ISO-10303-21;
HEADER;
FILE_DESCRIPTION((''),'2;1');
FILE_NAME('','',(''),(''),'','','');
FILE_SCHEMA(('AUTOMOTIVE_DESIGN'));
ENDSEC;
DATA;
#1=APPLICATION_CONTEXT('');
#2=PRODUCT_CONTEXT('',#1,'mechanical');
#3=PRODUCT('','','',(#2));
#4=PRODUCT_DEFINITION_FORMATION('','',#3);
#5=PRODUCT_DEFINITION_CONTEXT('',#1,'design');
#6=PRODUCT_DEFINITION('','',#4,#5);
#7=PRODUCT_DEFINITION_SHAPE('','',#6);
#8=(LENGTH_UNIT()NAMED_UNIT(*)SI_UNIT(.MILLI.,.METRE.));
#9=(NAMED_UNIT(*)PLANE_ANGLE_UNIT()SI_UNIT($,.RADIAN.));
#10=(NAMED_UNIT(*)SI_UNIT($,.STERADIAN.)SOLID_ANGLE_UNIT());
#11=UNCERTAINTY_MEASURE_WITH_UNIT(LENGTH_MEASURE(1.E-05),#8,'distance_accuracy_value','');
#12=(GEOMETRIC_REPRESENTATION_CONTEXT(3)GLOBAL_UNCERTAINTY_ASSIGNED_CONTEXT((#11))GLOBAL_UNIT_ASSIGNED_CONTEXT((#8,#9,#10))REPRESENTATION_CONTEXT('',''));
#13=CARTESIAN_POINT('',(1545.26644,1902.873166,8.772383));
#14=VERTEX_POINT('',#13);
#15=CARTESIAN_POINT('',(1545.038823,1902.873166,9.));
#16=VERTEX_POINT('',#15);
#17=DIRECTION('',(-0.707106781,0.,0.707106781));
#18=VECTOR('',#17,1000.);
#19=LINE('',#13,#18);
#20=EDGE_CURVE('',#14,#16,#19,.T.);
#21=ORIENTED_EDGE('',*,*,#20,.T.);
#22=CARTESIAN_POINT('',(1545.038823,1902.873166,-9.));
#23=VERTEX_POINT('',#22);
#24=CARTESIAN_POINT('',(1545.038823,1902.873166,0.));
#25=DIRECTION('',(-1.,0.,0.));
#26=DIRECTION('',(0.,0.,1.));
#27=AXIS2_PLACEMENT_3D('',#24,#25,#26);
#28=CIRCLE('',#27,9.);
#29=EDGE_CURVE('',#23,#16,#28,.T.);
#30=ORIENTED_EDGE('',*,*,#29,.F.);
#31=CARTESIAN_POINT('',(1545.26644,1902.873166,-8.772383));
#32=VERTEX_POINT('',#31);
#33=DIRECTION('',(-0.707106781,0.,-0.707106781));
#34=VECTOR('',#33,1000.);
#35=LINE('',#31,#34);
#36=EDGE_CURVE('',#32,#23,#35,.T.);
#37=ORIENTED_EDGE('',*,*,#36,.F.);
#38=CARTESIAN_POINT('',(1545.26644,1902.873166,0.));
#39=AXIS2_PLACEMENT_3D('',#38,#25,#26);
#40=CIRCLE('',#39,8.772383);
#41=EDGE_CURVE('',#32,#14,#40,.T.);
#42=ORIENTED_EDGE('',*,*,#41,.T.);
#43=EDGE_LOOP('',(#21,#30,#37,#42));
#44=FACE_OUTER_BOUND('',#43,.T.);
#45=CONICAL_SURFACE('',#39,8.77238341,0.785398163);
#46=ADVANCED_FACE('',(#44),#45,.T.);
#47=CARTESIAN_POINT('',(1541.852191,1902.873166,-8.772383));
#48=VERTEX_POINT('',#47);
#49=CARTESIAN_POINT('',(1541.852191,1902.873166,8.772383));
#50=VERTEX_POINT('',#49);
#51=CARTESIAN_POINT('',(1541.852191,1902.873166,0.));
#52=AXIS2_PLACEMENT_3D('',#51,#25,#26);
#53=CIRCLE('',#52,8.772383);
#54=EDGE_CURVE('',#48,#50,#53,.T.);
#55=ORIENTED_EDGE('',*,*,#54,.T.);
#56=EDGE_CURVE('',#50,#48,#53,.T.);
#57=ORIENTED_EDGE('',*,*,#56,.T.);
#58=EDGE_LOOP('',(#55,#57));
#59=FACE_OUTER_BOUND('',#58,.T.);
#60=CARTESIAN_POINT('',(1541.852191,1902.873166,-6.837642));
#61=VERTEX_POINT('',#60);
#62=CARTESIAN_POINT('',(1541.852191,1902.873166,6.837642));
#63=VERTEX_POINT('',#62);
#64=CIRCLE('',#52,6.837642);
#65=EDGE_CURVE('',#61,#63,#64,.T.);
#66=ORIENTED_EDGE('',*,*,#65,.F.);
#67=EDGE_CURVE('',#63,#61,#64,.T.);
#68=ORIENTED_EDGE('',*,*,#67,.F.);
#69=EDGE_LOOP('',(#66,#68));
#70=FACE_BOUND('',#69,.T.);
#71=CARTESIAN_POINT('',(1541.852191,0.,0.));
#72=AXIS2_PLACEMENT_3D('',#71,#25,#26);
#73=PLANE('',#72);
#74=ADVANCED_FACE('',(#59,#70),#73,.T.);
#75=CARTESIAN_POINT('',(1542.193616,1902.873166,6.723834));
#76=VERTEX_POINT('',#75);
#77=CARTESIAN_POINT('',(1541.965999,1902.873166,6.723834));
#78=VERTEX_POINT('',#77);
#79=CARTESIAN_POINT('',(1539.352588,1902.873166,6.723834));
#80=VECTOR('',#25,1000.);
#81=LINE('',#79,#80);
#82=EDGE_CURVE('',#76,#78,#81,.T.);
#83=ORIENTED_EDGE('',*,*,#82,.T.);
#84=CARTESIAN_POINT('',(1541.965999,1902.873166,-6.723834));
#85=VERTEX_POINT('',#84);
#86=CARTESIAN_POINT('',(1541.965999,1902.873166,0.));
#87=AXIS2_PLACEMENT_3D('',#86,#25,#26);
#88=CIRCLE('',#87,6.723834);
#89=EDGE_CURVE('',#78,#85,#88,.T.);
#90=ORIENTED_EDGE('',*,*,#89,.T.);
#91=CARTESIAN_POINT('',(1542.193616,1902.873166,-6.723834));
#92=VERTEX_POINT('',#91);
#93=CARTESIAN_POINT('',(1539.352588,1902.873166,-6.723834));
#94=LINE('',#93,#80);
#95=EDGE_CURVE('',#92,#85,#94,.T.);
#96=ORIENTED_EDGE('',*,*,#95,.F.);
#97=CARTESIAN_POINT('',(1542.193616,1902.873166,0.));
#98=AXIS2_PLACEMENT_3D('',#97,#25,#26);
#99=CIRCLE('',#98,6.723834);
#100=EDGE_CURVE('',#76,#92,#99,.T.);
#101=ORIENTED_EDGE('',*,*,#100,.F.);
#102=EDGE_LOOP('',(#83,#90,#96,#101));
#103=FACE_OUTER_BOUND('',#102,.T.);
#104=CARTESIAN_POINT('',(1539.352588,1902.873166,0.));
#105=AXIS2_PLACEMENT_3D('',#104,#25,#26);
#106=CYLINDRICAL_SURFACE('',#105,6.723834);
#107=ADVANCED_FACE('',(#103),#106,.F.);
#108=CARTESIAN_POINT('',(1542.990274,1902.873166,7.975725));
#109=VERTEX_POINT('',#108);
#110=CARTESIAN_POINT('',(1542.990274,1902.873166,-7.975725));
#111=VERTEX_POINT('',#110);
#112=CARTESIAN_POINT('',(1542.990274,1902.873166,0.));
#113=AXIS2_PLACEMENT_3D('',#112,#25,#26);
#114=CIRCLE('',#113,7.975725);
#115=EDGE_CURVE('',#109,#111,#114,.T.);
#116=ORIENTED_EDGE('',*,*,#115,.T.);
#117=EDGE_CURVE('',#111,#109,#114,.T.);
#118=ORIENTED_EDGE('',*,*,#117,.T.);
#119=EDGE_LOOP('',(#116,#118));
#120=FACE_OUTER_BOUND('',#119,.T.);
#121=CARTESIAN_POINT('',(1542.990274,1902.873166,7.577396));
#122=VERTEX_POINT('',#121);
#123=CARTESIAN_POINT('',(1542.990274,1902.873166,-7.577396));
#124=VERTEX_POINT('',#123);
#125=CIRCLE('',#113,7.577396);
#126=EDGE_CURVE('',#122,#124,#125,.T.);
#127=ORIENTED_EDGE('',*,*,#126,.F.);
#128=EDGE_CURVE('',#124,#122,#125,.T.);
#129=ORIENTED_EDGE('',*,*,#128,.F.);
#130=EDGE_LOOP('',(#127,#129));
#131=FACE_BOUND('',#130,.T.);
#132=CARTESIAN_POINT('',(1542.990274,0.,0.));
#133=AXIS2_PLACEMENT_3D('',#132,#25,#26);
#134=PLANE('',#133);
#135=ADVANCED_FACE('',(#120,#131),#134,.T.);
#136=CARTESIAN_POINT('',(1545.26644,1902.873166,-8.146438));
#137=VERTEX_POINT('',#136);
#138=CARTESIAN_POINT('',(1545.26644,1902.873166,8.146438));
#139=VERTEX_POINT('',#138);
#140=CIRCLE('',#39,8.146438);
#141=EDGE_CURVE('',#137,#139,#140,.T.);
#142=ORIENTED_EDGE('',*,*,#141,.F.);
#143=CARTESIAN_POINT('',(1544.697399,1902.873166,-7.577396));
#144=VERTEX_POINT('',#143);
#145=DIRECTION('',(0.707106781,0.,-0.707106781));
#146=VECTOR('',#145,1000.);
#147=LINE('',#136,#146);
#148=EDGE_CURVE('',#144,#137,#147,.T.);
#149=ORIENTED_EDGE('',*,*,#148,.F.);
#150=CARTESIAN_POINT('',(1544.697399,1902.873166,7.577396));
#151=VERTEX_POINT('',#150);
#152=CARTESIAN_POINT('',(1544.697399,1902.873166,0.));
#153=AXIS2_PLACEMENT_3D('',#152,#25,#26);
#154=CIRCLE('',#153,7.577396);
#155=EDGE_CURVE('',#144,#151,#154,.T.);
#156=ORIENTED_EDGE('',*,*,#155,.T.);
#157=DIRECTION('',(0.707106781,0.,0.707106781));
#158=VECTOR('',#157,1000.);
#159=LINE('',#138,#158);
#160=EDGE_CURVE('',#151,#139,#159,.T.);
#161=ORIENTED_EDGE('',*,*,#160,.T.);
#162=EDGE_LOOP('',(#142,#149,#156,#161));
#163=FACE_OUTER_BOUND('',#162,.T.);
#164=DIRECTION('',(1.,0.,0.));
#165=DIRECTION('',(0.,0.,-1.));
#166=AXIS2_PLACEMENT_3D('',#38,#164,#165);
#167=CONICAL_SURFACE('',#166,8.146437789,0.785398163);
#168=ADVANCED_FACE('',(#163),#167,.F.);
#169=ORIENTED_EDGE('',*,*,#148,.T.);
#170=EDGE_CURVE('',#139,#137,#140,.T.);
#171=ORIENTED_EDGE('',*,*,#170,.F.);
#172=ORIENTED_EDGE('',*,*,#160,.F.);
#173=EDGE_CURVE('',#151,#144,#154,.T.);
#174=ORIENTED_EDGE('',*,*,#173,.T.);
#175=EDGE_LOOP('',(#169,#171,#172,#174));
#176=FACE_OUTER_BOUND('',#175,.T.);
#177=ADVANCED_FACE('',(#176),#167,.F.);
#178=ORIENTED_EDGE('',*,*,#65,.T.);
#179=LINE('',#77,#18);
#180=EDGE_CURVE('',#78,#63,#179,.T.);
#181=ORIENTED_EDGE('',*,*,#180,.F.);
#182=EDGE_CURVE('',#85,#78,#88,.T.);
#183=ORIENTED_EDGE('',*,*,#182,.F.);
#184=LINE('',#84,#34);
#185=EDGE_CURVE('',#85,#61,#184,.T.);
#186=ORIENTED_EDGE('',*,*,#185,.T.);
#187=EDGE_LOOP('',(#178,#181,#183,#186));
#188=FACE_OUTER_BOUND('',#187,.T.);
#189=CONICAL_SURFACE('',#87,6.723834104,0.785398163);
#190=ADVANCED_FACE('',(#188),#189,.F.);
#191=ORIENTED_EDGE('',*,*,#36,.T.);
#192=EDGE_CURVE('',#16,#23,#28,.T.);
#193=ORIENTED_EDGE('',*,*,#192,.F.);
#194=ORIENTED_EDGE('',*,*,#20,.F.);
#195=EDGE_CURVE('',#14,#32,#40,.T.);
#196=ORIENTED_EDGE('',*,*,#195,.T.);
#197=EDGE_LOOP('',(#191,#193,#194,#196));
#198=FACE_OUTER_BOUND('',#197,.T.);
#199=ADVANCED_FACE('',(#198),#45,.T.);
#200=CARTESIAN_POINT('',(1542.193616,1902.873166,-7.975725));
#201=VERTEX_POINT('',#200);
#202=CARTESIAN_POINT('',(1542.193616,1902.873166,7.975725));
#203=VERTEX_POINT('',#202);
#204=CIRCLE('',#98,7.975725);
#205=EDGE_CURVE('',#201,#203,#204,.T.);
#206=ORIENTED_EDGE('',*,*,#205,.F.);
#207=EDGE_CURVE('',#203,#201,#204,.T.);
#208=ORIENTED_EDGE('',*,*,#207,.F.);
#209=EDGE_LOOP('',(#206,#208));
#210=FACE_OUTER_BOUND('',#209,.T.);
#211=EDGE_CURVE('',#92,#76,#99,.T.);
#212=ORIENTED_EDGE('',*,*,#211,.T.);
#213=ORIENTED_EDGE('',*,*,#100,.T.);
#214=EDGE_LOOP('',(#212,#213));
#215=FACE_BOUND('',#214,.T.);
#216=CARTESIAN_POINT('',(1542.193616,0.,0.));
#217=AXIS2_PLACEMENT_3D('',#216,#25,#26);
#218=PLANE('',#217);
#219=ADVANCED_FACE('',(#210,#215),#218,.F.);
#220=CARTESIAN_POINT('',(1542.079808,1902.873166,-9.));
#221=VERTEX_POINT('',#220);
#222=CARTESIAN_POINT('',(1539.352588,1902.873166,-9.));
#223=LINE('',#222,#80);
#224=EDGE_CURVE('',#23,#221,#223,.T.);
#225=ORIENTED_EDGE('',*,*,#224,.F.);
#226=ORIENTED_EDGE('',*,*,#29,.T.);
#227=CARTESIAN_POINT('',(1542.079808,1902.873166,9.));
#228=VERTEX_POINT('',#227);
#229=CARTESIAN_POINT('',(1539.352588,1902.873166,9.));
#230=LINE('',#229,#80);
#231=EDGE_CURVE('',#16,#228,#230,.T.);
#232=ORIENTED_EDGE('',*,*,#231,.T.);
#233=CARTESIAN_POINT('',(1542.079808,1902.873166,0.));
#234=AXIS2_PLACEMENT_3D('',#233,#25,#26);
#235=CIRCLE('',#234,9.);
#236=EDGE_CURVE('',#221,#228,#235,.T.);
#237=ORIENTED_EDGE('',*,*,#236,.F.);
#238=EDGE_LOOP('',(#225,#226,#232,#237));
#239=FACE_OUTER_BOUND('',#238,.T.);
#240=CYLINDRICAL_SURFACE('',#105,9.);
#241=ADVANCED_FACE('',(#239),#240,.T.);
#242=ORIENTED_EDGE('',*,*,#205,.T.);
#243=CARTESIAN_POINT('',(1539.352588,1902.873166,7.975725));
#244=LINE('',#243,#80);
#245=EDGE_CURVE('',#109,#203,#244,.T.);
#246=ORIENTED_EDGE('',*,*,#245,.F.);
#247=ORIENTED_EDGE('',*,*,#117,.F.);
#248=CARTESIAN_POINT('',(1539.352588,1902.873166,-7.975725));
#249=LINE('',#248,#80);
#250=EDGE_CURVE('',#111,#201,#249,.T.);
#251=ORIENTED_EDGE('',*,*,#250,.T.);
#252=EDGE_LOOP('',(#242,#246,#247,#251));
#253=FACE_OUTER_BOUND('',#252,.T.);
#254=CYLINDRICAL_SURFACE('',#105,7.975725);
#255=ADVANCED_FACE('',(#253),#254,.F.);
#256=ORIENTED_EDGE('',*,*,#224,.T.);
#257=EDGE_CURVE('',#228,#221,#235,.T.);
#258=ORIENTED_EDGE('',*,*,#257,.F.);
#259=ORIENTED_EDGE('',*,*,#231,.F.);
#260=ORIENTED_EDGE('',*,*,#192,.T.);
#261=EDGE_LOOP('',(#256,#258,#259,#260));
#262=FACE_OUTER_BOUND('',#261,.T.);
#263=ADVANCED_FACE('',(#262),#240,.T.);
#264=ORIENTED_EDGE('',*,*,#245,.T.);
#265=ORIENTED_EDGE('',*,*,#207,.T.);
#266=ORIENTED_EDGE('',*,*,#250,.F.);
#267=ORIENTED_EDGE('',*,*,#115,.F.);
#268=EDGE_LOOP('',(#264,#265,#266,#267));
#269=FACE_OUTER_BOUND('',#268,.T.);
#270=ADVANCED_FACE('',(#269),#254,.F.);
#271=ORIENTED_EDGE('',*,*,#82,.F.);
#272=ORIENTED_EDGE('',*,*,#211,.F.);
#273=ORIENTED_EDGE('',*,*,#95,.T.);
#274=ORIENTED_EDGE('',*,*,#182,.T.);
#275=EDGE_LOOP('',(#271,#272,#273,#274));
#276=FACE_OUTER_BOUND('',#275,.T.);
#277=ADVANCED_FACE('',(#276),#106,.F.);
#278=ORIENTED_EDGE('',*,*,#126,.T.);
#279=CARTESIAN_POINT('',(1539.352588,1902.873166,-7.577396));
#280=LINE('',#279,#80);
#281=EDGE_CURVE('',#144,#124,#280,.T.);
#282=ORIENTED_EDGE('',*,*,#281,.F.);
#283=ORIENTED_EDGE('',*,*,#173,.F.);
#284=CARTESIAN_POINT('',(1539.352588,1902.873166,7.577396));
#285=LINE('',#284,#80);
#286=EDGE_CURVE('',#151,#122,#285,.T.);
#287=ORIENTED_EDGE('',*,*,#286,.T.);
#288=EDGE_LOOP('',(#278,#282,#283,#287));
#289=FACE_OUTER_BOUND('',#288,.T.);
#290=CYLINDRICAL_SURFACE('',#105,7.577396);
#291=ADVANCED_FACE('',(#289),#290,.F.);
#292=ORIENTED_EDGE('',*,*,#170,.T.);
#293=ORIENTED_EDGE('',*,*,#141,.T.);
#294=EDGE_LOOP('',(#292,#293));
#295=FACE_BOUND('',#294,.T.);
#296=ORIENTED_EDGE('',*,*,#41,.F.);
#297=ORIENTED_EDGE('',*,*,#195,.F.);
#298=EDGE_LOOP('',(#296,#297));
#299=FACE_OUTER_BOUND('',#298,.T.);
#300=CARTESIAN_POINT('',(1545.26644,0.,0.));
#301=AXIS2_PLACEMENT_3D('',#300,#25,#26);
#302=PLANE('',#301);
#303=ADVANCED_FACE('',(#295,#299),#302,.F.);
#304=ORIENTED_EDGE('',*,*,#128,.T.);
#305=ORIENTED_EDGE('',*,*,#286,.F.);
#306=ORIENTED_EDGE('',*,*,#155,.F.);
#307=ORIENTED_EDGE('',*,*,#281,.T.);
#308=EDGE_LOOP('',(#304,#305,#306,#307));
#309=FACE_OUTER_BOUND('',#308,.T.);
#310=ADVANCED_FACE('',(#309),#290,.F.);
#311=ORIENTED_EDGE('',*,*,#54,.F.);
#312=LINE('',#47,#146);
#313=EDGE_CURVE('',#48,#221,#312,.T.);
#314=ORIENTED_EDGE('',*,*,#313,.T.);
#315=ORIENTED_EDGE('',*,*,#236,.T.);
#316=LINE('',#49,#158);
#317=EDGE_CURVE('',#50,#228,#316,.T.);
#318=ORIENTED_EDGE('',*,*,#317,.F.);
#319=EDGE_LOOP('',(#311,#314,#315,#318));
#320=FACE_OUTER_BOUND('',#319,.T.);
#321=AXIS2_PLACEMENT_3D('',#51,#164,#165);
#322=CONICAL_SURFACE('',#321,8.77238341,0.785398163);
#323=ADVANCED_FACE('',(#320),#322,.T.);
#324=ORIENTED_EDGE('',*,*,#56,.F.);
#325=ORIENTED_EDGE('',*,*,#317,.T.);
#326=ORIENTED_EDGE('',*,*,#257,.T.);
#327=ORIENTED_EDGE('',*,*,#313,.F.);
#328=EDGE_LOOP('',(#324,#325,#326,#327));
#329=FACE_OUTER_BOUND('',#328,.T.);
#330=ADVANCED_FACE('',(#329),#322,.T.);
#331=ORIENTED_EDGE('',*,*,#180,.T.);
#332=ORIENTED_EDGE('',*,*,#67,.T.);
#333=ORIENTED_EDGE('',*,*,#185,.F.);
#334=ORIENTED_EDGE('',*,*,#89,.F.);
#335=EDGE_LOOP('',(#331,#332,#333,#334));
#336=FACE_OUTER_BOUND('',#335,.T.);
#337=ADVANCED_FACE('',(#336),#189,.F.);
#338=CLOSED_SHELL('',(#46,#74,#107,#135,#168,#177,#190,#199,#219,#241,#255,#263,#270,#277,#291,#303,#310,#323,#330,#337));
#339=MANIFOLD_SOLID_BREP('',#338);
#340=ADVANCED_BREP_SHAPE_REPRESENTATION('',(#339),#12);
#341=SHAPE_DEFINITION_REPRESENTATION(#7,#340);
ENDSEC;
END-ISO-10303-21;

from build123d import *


with BuildPart() as part:
    # Sketch1 → Revolve1 (revolve)
    with BuildSketch(Plane.XY, mode=Mode.PRIVATE) as revolve1_sk:
        Polygon((1542.193616015, 1896.149332348), (1541.965999426, 1896.149332348), (1541.852191131, 1896.035524053), (1541.852191131, 1894.100783041), (1542.07980772, 1893.873166452), (1545.038823386, 1893.873166452), (1545.266439975, 1894.100783041), (1545.266439975, 1894.726728663), (1544.981919238, 1895.0112494), (1542.990274079, 1895.0112494), (1542.990274079, 1894.897441105), (1542.193616015, 1894.897441105), align=None)
        Polygon((1542.990274079, 1895.295770137), (1542.990274079, 1895.0112494), (1544.981919238, 1895.0112494), (1544.697398501, 1895.295770137), align=None)
    revolve(revolve1_sk.sketch.rotate(Axis((1539.352588353, 1902.873166452, 0), (1, 0, 0)), 270), axis=Axis((1539.352588353, 1902.873166452, 0), (1, 0, 0)))


solid = part.part
